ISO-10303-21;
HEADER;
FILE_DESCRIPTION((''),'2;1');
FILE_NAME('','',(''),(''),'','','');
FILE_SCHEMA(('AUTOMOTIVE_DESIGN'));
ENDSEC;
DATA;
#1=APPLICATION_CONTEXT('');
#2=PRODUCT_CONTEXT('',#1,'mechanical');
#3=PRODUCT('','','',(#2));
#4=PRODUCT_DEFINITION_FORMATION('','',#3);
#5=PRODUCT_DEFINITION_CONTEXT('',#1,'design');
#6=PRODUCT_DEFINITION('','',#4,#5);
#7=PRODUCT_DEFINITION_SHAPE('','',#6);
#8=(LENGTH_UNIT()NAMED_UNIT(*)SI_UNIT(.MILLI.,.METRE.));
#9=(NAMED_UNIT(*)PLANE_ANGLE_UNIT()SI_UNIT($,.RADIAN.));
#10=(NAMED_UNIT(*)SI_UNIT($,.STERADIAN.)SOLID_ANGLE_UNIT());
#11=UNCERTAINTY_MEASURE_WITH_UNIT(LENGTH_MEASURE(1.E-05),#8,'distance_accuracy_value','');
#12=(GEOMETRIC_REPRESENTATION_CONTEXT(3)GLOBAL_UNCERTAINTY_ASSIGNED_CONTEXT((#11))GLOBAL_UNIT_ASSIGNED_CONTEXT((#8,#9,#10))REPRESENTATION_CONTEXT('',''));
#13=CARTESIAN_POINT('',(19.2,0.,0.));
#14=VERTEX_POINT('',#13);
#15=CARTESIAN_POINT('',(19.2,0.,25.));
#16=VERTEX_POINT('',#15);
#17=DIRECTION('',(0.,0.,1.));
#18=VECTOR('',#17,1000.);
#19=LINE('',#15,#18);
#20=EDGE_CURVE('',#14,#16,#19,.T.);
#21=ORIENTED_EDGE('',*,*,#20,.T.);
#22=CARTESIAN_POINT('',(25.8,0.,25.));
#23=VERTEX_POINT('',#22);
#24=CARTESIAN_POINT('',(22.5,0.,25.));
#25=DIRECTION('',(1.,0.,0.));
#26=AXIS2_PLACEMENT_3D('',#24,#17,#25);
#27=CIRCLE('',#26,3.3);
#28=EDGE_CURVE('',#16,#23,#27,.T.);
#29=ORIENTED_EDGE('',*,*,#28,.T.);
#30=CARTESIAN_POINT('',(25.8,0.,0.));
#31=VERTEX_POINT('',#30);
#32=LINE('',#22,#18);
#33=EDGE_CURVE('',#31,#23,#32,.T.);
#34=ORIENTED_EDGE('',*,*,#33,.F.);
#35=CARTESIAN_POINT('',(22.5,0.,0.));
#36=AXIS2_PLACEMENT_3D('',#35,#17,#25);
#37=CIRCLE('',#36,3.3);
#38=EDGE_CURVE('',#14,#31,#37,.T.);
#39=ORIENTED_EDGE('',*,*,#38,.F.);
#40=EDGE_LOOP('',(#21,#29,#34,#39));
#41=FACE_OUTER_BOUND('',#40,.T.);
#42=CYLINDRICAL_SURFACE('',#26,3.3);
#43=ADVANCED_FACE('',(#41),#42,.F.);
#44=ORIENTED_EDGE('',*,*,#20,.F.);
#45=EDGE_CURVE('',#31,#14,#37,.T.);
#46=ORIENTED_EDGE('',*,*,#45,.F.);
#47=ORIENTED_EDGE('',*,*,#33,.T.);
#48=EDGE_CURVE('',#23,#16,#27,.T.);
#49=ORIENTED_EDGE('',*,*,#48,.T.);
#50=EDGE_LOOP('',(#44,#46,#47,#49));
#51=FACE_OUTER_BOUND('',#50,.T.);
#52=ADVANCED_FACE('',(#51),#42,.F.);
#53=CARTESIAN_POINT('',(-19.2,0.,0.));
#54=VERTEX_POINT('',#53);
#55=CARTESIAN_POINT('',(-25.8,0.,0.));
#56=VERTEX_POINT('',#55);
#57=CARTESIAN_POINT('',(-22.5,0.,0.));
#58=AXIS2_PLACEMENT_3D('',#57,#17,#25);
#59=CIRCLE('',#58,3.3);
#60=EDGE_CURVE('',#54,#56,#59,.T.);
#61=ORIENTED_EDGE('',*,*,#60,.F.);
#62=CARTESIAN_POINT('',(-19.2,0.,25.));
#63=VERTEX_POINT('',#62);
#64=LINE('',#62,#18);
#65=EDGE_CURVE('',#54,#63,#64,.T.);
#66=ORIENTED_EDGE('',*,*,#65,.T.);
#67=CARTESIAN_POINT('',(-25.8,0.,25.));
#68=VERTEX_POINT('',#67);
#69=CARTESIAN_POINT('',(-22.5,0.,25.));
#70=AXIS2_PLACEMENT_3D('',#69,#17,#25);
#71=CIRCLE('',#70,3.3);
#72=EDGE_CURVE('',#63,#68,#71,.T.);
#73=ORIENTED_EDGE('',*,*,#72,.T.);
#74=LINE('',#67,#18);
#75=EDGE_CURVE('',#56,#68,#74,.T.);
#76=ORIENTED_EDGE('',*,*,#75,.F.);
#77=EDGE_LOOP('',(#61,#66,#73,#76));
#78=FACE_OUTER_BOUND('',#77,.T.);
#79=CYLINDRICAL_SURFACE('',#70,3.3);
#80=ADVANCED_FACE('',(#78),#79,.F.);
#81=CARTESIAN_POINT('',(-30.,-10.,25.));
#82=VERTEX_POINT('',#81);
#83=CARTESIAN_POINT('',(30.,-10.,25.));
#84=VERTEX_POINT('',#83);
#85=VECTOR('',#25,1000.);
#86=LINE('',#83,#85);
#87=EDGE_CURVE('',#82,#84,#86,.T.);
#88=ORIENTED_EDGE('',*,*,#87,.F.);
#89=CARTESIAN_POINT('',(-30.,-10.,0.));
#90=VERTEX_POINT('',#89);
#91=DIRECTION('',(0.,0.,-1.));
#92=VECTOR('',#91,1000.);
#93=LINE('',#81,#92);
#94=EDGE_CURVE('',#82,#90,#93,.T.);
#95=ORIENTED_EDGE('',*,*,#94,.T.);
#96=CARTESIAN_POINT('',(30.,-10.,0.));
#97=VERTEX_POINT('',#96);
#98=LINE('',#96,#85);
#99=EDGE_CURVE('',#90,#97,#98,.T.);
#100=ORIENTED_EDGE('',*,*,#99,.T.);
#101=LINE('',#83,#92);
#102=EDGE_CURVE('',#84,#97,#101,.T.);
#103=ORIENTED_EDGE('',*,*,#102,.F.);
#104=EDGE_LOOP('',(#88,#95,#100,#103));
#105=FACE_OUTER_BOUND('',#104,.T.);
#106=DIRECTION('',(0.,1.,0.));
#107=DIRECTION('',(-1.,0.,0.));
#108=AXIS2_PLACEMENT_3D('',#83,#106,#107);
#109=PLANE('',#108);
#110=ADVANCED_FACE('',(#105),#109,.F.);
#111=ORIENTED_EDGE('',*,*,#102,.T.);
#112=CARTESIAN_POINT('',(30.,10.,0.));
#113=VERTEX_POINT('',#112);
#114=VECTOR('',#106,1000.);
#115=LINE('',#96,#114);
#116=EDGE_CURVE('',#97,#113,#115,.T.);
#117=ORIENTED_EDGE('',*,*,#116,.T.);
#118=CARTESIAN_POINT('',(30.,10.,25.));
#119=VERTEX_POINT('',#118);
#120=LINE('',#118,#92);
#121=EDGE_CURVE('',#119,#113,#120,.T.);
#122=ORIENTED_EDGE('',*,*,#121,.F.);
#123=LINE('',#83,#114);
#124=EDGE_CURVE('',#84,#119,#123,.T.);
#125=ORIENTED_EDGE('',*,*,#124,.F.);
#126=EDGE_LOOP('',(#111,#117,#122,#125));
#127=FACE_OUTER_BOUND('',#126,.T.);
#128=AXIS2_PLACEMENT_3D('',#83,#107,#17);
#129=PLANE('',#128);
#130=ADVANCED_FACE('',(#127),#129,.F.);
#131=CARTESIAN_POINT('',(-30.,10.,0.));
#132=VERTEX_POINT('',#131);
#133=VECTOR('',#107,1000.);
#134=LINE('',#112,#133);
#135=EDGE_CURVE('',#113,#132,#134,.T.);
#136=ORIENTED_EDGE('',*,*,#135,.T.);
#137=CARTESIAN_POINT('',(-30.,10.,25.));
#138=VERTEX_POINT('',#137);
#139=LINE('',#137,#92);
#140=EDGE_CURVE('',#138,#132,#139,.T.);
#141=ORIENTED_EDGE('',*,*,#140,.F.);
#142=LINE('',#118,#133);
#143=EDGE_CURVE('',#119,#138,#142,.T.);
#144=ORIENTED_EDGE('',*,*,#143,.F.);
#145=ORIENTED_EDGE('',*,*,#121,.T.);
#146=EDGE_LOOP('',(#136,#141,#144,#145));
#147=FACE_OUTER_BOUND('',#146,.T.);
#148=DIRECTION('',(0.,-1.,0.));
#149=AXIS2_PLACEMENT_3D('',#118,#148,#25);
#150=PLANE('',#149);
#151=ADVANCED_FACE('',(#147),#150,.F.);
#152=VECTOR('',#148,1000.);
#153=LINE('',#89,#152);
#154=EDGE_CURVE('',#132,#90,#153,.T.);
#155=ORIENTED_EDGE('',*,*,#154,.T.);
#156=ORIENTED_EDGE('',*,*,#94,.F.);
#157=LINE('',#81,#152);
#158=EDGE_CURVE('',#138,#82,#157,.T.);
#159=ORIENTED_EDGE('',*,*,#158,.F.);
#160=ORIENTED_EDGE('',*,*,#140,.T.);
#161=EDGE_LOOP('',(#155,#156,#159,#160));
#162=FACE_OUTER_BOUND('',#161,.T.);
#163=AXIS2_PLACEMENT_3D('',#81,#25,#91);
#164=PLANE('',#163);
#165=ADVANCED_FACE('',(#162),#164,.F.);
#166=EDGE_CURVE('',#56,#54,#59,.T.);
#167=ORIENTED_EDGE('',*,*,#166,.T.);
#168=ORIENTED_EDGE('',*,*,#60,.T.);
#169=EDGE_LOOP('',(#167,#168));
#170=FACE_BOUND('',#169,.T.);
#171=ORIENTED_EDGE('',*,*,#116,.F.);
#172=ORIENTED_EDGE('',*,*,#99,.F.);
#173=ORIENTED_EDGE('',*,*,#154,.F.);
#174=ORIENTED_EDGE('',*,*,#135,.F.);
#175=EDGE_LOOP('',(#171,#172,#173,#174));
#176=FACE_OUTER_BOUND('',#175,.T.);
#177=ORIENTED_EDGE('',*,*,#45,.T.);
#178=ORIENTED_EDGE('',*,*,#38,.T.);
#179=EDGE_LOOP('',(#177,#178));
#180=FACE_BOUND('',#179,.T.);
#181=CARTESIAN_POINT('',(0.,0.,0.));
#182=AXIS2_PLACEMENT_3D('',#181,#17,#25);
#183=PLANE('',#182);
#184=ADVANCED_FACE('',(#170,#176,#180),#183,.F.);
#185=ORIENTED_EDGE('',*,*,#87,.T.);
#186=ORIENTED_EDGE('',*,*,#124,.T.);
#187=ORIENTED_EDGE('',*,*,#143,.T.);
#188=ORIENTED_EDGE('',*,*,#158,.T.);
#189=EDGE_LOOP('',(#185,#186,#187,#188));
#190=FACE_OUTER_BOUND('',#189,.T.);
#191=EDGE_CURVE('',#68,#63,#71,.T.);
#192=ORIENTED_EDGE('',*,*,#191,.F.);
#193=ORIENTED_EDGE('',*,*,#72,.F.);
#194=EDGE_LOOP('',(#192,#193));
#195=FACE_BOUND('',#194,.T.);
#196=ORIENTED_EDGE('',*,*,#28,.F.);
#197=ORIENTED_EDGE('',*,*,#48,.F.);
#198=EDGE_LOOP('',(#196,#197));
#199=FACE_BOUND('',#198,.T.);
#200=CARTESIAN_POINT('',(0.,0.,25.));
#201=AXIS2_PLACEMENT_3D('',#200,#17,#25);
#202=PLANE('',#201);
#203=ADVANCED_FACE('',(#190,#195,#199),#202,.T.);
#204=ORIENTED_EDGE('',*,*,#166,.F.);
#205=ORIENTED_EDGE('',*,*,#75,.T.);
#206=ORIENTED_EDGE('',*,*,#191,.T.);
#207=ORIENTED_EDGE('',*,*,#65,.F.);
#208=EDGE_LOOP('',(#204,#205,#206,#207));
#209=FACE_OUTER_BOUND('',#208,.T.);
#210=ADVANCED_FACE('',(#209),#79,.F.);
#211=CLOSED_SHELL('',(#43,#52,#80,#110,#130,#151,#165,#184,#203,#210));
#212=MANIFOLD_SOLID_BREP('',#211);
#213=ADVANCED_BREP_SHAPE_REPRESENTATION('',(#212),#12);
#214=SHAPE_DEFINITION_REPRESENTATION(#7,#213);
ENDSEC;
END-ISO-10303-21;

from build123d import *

# Parameters (mm, degrees)
SKETCH_1_W         = 60
SKETCH_1_H         = 20
EXTRUDE_1_DEPTH    = 25
HOLE_WIZARD_M6_1_D = 6.6


with BuildPart() as part:
    # 草图1 → 凸台-拉伸1 (new body)
    with BuildSketch(Plane.XY):
        Rectangle(SKETCH_1_W, SKETCH_1_H)
    extrude(amount=EXTRUDE_1_DEPTH)

    # M6 间隙孔1 (through all)
    with Locations(Plane.XY.offset(25)):
        with Locations((-22.5, 0), (22.5, 0)):
            Hole(HOLE_WIZARD_M6_1_D / 2)


solid = part.part
